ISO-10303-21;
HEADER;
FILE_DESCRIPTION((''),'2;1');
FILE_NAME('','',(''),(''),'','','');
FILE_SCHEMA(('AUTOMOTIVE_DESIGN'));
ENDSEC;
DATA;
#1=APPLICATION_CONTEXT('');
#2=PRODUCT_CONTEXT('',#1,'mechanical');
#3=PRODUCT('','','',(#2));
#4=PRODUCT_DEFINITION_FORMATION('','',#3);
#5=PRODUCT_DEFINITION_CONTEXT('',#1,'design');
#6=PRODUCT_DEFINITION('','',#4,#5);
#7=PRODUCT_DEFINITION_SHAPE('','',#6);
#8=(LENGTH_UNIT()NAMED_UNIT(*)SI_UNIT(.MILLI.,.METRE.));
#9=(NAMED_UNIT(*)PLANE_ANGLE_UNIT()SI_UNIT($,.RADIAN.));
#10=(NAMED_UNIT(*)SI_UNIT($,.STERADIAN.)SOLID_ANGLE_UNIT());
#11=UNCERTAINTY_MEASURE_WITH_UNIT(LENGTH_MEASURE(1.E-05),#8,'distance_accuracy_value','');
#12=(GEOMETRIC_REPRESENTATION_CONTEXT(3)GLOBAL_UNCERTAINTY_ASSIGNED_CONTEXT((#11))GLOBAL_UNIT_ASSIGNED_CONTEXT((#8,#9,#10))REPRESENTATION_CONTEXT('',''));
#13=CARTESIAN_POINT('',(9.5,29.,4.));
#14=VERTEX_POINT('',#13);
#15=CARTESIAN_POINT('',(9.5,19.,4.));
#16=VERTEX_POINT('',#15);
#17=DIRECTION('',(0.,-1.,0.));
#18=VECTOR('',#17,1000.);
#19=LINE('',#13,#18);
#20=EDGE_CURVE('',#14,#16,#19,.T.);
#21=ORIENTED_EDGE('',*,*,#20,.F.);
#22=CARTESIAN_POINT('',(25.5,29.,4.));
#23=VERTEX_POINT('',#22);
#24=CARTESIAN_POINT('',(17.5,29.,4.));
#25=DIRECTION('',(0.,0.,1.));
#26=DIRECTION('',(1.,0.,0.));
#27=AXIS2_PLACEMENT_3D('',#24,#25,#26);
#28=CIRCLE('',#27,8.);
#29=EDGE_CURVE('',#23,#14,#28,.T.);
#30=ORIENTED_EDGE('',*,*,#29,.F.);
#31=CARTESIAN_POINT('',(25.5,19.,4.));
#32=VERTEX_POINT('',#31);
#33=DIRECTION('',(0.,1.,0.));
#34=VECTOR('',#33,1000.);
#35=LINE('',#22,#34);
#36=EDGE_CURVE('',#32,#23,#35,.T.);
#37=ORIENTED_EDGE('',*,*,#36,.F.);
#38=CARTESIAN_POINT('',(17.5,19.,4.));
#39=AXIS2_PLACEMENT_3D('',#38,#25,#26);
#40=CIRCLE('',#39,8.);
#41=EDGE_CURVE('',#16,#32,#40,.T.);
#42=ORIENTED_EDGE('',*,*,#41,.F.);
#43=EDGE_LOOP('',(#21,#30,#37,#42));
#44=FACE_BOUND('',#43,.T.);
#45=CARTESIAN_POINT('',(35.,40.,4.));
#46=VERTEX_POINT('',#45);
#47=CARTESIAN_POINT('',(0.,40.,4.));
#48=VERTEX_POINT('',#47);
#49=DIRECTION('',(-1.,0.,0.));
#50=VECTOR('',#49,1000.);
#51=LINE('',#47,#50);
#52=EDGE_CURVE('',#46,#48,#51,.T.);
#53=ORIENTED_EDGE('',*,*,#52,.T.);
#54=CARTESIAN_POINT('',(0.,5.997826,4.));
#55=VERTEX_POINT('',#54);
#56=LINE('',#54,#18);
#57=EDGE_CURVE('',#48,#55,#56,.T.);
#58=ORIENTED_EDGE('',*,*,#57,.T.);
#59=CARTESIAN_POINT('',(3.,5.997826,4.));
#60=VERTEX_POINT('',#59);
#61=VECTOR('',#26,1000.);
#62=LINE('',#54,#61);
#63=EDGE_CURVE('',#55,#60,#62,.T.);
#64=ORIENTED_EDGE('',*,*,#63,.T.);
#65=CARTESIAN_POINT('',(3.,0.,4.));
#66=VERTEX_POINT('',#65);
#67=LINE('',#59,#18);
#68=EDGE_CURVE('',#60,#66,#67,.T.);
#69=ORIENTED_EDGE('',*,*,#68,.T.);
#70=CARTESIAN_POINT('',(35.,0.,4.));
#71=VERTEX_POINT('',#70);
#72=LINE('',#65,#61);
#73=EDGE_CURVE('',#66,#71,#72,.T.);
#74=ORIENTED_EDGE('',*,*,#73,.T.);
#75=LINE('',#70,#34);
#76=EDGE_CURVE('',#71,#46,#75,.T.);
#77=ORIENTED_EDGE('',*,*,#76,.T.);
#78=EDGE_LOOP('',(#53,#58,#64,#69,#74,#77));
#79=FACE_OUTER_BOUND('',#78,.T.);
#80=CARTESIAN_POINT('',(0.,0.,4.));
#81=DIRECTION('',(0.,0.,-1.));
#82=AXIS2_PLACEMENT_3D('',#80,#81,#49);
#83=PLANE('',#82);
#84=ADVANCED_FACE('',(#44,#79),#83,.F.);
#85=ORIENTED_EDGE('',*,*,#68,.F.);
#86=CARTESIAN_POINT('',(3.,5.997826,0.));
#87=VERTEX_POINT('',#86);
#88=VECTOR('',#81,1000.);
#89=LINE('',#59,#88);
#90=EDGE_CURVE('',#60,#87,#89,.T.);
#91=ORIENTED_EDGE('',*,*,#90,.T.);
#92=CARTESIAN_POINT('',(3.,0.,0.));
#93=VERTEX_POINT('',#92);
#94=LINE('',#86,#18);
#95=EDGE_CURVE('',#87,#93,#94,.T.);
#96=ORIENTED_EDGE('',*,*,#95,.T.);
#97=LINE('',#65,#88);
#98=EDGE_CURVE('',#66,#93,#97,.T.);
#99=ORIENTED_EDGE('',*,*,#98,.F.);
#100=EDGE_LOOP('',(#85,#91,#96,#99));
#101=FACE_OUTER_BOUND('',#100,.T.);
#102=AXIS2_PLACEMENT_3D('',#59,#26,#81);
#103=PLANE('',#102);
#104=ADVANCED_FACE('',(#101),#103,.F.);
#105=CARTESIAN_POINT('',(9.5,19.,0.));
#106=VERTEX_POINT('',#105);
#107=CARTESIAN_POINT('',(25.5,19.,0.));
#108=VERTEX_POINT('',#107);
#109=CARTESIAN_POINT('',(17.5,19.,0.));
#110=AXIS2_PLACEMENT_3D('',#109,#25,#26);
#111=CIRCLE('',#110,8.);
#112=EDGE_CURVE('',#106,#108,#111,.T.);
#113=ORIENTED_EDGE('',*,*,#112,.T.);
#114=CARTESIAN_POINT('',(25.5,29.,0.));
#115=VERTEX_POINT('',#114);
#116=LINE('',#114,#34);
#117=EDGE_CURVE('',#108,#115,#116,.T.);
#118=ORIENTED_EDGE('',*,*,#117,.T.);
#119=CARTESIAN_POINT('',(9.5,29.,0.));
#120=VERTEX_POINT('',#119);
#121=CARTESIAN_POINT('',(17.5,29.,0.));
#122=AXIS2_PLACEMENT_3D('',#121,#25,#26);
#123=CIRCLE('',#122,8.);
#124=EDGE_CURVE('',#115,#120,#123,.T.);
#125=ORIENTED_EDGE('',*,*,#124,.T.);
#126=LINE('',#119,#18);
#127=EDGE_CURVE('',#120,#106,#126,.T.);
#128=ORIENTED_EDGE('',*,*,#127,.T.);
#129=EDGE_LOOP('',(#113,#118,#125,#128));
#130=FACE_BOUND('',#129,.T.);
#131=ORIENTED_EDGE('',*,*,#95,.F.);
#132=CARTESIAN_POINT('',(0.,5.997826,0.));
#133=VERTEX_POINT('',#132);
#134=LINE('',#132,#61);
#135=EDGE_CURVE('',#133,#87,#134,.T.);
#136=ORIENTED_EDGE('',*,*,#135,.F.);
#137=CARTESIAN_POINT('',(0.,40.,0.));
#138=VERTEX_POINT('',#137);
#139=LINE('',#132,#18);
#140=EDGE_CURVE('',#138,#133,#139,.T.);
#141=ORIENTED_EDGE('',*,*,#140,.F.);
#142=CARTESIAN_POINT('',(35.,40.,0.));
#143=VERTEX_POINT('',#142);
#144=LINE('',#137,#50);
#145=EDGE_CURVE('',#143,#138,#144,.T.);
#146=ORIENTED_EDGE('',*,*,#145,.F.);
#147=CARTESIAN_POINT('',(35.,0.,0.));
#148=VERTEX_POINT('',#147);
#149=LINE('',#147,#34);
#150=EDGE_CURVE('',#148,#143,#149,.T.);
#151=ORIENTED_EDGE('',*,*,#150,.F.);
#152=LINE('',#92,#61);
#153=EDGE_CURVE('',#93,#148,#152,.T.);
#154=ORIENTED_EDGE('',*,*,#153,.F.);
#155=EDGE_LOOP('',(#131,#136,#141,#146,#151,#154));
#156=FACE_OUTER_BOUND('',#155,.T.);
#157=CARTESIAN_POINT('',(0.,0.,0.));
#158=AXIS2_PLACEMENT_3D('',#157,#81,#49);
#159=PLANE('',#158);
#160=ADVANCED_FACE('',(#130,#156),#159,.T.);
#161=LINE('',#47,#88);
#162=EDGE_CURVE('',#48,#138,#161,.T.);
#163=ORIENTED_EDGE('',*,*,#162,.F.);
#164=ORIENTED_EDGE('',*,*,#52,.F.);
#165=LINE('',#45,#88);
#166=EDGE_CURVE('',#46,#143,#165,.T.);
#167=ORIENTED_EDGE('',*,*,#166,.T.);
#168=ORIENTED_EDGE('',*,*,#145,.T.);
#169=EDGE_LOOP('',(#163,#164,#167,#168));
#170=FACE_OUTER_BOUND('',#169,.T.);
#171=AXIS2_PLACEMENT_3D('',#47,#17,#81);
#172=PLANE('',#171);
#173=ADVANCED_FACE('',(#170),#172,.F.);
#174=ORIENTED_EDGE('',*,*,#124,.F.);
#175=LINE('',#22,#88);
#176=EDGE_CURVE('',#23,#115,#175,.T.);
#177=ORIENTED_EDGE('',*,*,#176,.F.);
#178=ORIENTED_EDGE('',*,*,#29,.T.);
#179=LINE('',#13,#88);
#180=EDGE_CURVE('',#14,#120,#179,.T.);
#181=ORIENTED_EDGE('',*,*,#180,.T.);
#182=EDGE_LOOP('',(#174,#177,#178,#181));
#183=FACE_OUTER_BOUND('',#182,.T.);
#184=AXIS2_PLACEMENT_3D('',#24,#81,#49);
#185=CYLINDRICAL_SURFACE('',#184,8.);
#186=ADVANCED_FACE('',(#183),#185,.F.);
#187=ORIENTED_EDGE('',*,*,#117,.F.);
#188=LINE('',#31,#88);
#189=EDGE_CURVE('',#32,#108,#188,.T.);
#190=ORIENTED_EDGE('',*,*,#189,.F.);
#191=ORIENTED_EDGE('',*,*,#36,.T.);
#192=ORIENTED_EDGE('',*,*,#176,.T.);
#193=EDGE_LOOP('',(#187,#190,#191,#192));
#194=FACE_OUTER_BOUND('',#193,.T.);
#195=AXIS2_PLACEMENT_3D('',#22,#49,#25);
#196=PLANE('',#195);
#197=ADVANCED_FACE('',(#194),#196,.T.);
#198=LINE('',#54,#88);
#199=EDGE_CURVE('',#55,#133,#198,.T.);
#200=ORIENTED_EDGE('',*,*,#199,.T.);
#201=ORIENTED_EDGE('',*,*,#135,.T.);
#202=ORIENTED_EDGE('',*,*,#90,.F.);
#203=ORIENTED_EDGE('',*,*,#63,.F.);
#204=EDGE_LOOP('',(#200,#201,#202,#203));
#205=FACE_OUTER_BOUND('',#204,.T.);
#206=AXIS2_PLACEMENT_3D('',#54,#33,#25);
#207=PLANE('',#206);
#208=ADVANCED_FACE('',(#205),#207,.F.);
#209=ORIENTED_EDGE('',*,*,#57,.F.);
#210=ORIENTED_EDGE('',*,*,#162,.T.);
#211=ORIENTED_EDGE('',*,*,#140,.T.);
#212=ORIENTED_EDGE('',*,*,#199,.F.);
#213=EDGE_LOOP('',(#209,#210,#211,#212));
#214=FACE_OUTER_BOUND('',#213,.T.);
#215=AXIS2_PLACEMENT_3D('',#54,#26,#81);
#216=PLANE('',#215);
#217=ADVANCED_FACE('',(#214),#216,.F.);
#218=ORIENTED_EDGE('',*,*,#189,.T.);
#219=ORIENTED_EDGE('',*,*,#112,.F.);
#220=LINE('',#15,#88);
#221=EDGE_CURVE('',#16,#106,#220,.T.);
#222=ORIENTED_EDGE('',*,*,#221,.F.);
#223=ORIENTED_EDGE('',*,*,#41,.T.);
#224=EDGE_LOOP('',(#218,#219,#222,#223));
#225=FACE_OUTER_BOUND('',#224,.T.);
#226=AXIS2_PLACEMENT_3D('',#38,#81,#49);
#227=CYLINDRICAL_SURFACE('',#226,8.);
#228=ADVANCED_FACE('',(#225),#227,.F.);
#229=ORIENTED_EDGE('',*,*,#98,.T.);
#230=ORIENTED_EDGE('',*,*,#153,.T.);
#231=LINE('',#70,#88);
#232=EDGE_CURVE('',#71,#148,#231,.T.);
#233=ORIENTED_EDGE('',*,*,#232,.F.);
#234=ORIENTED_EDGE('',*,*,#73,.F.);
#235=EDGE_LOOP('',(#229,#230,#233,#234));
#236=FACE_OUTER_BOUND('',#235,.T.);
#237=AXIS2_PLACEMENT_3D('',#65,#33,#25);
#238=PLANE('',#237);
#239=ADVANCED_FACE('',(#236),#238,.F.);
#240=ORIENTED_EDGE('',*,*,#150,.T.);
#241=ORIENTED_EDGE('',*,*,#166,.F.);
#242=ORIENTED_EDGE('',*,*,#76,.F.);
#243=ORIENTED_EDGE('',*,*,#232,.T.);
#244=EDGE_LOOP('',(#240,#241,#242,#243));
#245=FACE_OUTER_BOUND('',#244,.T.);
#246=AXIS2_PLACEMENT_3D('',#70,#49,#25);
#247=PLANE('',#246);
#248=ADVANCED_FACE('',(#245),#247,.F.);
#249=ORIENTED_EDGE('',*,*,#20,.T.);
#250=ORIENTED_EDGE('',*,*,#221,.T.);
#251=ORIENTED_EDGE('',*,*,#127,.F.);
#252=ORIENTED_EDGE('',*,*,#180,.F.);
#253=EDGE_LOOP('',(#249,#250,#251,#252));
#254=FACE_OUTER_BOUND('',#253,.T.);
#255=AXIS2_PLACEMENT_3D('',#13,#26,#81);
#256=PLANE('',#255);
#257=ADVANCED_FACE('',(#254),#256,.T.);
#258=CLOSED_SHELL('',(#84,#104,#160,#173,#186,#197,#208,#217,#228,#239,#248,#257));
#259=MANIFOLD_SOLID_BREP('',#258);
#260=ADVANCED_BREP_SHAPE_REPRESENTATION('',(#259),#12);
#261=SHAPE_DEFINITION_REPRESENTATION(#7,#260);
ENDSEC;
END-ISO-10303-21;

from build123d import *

# Parameters (mm, degrees)
BOSS_EXTRUDE1_DEPTH = 4


with BuildPart() as part:
    # Sketch1 → Boss-Extrude1 (new body)
    with BuildSketch(Plane.XY):
        Polygon((3, 0), (35, 0), (35, 40), (0, 40), (0, 5.997826072), (3, 5.997826072), align=None)
        with BuildLine():
            Line((9.5, 29), (9.5, 19))
            ThreePointArc((9.5, 19), (17.5, 11), (25.5, 19))
            Line((25.5, 19), (25.5, 29))
            ThreePointArc((25.5, 29), (17.5, 37), (9.5, 29))
        make_face(mode=Mode.SUBTRACT)
    extrude(amount=BOSS_EXTRUDE1_DEPTH)


solid = part.part
